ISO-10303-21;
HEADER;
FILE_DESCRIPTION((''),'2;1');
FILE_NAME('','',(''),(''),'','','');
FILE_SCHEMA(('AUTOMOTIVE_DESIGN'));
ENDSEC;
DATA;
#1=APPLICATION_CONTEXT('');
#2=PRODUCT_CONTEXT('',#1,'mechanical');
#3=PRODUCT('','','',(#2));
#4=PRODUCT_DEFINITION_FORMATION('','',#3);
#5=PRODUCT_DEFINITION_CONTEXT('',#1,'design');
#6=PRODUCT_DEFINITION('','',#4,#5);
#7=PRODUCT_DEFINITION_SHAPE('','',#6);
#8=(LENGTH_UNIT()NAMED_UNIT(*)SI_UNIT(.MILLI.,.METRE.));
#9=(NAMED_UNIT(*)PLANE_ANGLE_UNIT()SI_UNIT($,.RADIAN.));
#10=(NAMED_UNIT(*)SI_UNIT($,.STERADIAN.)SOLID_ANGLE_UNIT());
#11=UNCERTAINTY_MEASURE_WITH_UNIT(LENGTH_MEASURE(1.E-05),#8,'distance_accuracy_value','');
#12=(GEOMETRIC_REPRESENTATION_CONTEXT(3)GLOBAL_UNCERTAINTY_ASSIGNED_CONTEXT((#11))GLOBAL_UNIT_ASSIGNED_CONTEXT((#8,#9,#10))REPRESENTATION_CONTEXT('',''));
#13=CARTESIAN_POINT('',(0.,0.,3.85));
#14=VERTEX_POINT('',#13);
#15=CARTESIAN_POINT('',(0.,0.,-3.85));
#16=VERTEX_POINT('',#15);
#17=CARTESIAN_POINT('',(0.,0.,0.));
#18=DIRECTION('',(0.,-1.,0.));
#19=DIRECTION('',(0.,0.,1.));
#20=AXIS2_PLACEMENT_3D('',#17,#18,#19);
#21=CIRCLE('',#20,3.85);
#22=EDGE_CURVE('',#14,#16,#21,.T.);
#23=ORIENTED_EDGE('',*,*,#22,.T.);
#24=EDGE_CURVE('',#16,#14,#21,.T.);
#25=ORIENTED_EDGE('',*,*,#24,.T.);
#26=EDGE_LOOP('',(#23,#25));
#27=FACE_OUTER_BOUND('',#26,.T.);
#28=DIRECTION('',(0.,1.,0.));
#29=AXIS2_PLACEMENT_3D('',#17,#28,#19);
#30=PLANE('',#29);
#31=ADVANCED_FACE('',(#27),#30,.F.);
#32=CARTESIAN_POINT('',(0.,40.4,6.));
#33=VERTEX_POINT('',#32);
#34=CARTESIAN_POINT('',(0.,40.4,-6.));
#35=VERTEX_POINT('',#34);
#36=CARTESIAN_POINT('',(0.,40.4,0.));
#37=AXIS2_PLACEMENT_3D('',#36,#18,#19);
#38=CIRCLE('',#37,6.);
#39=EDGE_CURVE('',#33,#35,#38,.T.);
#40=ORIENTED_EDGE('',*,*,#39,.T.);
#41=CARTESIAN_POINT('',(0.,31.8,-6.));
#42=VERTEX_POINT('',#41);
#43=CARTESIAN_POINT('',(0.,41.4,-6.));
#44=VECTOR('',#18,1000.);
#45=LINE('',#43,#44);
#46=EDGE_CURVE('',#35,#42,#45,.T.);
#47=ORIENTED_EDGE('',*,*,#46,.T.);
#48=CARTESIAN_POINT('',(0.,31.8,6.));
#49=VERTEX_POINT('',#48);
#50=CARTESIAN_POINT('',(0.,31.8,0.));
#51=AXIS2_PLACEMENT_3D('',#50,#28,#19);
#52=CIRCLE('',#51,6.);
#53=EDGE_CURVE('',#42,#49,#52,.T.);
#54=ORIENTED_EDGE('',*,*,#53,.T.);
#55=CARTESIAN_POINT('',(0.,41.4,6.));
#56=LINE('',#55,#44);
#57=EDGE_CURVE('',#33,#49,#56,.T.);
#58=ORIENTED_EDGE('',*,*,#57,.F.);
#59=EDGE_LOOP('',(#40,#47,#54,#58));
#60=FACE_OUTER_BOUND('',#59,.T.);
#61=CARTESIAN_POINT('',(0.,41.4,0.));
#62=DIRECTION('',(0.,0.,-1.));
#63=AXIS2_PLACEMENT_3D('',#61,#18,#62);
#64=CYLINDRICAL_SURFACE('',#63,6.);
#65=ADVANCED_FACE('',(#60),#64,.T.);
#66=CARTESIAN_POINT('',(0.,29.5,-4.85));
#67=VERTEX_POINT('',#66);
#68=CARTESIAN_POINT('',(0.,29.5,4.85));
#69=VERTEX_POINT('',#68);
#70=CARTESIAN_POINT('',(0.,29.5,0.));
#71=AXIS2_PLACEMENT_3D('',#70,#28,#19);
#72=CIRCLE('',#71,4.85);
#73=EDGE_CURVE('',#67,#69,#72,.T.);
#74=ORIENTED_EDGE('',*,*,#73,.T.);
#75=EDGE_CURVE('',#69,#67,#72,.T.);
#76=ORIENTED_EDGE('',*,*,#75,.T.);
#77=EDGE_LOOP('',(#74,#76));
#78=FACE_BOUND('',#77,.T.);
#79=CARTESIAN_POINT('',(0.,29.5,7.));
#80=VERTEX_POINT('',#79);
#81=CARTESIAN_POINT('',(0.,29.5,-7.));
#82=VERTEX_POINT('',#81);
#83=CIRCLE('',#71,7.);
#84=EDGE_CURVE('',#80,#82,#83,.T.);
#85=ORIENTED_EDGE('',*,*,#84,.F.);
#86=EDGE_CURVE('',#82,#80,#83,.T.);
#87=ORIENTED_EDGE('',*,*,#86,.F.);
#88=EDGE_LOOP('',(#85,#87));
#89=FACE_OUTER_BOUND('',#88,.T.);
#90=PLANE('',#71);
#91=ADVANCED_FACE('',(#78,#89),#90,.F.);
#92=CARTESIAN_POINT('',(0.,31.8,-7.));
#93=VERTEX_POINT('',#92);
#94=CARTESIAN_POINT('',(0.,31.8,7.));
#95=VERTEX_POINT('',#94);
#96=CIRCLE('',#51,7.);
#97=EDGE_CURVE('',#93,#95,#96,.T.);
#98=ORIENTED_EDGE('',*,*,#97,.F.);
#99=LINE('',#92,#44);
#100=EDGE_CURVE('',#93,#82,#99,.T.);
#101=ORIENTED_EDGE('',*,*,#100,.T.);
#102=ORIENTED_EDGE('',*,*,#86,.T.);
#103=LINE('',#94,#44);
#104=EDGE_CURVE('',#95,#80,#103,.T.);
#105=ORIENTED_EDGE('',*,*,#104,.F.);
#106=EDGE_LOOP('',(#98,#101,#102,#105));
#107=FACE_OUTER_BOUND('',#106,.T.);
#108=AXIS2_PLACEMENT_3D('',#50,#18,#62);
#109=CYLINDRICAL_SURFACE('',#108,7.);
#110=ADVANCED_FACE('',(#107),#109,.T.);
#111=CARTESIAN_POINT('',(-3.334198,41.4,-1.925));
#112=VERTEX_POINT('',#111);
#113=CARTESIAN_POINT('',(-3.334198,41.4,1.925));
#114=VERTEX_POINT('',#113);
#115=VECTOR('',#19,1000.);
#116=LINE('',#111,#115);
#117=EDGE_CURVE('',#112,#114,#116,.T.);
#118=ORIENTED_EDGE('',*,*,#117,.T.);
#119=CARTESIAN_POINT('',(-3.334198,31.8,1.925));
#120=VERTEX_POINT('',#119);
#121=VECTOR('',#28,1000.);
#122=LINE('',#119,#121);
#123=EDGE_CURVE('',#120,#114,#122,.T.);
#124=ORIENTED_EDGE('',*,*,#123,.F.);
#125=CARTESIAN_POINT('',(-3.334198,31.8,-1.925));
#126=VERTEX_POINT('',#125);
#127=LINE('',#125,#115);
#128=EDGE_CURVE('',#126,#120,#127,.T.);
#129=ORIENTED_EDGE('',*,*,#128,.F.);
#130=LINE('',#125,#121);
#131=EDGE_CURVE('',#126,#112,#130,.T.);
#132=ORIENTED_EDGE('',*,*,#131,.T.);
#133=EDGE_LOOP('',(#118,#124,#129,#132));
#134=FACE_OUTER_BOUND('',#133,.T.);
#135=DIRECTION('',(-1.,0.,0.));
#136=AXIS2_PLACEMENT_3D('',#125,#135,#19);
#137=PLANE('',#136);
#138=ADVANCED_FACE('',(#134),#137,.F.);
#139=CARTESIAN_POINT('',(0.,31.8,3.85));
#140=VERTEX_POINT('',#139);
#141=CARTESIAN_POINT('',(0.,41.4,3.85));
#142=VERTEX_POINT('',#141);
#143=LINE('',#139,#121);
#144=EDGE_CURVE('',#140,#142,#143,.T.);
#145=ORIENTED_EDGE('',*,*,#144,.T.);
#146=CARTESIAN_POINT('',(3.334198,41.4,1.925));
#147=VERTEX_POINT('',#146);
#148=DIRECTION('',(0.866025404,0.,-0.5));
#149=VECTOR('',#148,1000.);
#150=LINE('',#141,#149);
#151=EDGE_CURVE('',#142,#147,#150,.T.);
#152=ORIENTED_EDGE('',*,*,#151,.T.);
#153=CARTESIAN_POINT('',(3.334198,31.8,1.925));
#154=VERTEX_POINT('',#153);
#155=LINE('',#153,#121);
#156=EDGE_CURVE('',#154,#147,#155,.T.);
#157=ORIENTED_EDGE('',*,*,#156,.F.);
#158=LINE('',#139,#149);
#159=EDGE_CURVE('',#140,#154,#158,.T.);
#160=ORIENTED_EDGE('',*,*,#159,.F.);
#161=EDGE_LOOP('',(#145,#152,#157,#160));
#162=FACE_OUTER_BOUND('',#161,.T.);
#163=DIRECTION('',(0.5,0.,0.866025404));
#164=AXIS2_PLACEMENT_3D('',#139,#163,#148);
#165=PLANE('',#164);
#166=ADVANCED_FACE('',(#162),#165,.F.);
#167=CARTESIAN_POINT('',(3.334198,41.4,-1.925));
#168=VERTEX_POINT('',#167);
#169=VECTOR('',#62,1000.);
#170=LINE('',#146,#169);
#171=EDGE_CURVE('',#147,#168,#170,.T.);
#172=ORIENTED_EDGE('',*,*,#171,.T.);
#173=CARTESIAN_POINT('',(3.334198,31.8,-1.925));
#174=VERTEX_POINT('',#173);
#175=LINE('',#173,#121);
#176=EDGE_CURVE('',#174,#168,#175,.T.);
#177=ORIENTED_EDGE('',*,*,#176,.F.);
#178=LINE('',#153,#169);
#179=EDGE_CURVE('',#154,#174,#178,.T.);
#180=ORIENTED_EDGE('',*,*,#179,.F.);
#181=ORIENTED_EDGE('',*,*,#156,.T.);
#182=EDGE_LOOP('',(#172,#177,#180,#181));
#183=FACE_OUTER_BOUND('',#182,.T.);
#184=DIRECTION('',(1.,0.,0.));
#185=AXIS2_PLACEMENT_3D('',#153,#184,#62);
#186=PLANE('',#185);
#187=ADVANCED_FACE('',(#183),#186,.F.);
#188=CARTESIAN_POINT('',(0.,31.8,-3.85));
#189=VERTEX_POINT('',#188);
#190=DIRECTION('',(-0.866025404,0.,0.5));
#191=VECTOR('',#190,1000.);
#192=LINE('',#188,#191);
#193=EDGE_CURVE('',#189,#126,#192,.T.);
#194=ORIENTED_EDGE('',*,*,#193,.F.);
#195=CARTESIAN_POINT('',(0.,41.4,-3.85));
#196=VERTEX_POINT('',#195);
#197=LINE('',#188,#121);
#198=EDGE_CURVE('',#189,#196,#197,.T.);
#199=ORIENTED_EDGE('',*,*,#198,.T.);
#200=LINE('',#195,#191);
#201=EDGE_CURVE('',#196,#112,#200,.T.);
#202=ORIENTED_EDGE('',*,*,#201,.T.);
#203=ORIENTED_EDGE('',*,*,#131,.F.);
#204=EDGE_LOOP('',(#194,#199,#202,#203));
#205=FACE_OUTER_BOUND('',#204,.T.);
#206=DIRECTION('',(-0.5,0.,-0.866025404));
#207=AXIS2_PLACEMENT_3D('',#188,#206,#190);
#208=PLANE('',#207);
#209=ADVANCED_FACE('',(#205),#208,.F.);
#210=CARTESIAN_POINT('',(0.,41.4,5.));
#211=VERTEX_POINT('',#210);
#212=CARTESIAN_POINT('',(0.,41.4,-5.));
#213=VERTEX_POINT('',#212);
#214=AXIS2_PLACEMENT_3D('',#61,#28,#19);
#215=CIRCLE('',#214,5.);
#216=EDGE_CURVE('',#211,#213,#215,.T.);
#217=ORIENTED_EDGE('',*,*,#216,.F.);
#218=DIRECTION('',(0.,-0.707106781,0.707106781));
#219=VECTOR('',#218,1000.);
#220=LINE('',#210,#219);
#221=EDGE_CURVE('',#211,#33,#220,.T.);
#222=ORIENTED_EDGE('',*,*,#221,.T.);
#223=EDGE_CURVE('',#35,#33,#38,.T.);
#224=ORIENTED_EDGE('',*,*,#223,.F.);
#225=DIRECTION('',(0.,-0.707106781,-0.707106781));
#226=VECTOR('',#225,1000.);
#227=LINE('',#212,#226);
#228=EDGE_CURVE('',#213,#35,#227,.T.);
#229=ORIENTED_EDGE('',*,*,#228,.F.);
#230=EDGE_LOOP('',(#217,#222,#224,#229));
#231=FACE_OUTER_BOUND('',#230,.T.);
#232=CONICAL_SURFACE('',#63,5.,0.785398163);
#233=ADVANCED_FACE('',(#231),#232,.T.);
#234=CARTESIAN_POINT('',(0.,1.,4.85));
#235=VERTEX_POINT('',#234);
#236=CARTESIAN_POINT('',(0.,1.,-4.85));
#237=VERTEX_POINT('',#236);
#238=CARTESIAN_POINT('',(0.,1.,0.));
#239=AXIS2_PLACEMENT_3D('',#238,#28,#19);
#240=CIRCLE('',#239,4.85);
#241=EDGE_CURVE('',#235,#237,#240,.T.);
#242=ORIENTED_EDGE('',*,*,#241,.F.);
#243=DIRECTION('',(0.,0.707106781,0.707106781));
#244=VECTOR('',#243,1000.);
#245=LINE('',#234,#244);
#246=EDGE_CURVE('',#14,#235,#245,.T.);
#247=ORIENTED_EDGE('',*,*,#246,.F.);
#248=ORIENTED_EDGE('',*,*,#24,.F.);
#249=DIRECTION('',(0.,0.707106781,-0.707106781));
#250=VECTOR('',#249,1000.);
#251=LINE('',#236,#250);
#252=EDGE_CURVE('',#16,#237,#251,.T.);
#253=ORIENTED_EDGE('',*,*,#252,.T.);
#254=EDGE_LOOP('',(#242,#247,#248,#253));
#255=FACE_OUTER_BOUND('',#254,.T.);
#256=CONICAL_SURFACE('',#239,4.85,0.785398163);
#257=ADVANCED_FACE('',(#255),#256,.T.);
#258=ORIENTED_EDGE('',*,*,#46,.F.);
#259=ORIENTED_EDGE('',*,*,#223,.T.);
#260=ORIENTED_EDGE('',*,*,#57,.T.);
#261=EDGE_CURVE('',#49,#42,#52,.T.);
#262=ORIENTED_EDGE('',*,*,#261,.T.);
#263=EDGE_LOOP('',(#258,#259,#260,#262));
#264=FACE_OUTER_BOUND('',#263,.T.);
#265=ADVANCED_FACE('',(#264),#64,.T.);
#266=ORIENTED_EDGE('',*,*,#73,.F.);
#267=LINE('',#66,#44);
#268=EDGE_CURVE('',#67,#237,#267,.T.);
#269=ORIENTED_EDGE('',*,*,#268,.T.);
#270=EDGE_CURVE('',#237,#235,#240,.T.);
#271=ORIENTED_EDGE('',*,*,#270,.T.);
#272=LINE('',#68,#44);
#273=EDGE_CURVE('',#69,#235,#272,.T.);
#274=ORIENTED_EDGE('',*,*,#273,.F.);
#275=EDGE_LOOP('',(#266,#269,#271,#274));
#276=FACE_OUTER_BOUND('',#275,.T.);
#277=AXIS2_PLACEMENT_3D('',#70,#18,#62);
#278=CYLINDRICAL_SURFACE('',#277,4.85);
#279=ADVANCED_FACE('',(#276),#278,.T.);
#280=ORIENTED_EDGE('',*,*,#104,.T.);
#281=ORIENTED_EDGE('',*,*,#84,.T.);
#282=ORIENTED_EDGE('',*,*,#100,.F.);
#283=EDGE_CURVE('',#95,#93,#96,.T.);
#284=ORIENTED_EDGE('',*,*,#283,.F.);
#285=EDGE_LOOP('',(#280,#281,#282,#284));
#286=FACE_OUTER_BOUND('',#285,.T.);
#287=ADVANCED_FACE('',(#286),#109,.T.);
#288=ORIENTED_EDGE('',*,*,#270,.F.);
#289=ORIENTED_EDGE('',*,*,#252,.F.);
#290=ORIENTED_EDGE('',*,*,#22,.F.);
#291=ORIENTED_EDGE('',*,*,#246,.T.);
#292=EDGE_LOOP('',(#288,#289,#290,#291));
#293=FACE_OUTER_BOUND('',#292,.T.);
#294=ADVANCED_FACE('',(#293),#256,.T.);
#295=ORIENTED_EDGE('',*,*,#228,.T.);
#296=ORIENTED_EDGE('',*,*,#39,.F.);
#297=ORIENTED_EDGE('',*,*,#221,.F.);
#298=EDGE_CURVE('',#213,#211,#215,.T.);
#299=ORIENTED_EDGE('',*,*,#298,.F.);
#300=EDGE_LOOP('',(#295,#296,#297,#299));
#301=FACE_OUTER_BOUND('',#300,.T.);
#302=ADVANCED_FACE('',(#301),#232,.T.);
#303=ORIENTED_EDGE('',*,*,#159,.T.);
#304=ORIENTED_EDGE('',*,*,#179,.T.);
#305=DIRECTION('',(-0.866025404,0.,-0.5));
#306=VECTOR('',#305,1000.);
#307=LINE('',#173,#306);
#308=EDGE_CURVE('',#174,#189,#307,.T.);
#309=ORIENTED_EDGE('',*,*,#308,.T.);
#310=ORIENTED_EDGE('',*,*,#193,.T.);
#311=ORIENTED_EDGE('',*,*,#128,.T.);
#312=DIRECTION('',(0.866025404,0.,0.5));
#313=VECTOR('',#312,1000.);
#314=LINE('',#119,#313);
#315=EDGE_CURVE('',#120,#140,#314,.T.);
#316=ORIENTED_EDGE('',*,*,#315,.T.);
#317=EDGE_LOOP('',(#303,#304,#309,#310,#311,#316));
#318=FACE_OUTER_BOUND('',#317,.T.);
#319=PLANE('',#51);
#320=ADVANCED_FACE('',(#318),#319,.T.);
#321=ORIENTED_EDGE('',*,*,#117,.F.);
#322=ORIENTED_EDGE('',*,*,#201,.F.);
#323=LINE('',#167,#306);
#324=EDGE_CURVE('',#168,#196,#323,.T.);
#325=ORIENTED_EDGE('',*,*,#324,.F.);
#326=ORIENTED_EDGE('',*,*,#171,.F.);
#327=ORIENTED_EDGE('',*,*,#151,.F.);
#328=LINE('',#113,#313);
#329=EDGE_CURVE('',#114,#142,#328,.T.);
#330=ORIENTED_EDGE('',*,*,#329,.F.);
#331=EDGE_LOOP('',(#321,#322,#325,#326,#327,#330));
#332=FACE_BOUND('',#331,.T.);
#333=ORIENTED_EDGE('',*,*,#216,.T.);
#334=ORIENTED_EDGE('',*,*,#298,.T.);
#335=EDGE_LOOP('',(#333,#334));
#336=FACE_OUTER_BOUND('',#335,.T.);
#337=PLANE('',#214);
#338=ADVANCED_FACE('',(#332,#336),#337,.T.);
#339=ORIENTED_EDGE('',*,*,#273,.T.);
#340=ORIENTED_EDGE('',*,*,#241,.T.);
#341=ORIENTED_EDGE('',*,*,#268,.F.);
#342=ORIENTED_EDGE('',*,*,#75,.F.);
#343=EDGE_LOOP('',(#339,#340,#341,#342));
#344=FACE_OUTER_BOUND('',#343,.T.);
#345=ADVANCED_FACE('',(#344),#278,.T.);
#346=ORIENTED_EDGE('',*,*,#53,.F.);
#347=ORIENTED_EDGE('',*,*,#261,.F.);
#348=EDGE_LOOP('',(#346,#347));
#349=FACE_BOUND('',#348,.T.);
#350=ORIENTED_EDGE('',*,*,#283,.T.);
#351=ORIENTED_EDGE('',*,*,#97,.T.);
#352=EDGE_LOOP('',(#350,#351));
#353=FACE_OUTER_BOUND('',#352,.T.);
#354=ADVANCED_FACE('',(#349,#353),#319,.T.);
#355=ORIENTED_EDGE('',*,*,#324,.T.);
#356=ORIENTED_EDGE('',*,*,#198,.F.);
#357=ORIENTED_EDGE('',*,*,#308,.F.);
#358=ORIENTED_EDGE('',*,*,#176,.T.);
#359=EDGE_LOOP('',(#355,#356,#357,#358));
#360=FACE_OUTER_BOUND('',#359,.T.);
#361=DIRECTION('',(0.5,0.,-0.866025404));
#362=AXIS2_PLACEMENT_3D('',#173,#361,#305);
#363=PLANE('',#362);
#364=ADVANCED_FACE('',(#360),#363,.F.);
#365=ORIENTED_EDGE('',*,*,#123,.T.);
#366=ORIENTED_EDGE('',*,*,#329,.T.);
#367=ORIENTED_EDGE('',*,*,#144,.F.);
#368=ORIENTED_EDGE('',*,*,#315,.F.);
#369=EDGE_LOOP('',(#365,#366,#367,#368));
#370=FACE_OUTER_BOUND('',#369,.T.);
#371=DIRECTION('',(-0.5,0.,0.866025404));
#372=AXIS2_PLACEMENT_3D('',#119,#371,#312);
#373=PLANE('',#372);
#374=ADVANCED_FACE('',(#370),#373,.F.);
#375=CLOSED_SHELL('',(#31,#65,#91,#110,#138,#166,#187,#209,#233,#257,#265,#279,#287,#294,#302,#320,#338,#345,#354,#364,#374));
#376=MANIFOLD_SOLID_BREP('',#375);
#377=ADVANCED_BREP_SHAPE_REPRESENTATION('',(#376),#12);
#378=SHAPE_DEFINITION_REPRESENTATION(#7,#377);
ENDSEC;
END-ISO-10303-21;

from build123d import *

# Parameters (mm, degrees)
SHANK_SKETCH_9_7_R            = 4.85
SHANK_9_7X29_5_DEPTH          = 29.5
FLANGE_SKETCH_17_3_R          = 7
FLANGE_17_3X2_3_DEPTH         = 2.3
HEAD_SKETCH_12_R              = 6
HEAD_12X9_6_DEPTH             = 9.6
HEX_SOCKET_7_7X9_6_DEEP_DEPTH = 9.6
HEAD_TOP_CHAMFER_1X45_SIZE    = 1
SHANK_END_CHAMFER_1X45_SIZE   = 1


with BuildPart() as part:
    # Shank Sketch Ø9.7 → Shank Ø9.7x29.5 (new body)
    with BuildSketch(Plane(origin=(0, 0, 0), x_dir=(1, 0, 0), z_dir=(0, 1, 0))):
        with Locations(Location((0, 0, 0), (0, 0, 270))):
            Circle(SHANK_SKETCH_9_7_R)
    extrude(amount=SHANK_9_7X29_5_DEPTH)

    # Flange Sketch Ø17.3 → Flange Ø17.3x2.3 (add)
    with BuildSketch(Plane(origin=(0, 29.5, 0), x_dir=(1, 0, 0), z_dir=(0, 1, 0))):
        with Locations(Location((0, 0, 0), (0, 0, 270))):
            Circle(FLANGE_SKETCH_17_3_R)
    extrude(amount=FLANGE_17_3X2_3_DEPTH)

    # Head Sketch Ø12 → Head Ø12x9.6 (add)
    with BuildSketch(Plane(origin=(0, 31.8, 0), x_dir=(1, 0, 0), z_dir=(0, 1, 0))):
        with Locations(Location((0, 0, 0), (0, 0, 270))):
            Circle(HEAD_SKETCH_12_R)
    extrude(amount=HEAD_12X9_6_DEPTH)

    # Hex Socket Sketch 7.7 → Hex Socket 7.7x9.6 Deep (cut)
    with BuildSketch(Plane(origin=(0, 41.4, 0), x_dir=(1, 0, 0), z_dir=(0, 1, 0))):
        Polygon((0, 3.85), (-3.334197805, 1.925), (-3.334197805, -1.925), (0, -3.85), (3.334197805, -1.925), (3.334197805, 1.925), align=None)
    extrude(amount=-HEX_SOCKET_7_7X9_6_DEEP_DEPTH, mode=Mode.SUBTRACT)

    # Head Top Chamfer 1x45
    head_top_chamfer_1x45_edges = [part.edges().sort_by_distance(p)[0] for p in [
        (0, 41.4, -6),
    ]]
    chamfer(head_top_chamfer_1x45_edges, length=HEAD_TOP_CHAMFER_1X45_SIZE)

    # Shank End Chamfer 1x45
    shank_end_chamfer_1x45_edges = [part.edges().sort_by_distance(p)[0] for p in [
        (0, 0, -4.85),
    ]]
    chamfer(shank_end_chamfer_1x45_edges, length=SHANK_END_CHAMFER_1X45_SIZE)


solid = part.part
